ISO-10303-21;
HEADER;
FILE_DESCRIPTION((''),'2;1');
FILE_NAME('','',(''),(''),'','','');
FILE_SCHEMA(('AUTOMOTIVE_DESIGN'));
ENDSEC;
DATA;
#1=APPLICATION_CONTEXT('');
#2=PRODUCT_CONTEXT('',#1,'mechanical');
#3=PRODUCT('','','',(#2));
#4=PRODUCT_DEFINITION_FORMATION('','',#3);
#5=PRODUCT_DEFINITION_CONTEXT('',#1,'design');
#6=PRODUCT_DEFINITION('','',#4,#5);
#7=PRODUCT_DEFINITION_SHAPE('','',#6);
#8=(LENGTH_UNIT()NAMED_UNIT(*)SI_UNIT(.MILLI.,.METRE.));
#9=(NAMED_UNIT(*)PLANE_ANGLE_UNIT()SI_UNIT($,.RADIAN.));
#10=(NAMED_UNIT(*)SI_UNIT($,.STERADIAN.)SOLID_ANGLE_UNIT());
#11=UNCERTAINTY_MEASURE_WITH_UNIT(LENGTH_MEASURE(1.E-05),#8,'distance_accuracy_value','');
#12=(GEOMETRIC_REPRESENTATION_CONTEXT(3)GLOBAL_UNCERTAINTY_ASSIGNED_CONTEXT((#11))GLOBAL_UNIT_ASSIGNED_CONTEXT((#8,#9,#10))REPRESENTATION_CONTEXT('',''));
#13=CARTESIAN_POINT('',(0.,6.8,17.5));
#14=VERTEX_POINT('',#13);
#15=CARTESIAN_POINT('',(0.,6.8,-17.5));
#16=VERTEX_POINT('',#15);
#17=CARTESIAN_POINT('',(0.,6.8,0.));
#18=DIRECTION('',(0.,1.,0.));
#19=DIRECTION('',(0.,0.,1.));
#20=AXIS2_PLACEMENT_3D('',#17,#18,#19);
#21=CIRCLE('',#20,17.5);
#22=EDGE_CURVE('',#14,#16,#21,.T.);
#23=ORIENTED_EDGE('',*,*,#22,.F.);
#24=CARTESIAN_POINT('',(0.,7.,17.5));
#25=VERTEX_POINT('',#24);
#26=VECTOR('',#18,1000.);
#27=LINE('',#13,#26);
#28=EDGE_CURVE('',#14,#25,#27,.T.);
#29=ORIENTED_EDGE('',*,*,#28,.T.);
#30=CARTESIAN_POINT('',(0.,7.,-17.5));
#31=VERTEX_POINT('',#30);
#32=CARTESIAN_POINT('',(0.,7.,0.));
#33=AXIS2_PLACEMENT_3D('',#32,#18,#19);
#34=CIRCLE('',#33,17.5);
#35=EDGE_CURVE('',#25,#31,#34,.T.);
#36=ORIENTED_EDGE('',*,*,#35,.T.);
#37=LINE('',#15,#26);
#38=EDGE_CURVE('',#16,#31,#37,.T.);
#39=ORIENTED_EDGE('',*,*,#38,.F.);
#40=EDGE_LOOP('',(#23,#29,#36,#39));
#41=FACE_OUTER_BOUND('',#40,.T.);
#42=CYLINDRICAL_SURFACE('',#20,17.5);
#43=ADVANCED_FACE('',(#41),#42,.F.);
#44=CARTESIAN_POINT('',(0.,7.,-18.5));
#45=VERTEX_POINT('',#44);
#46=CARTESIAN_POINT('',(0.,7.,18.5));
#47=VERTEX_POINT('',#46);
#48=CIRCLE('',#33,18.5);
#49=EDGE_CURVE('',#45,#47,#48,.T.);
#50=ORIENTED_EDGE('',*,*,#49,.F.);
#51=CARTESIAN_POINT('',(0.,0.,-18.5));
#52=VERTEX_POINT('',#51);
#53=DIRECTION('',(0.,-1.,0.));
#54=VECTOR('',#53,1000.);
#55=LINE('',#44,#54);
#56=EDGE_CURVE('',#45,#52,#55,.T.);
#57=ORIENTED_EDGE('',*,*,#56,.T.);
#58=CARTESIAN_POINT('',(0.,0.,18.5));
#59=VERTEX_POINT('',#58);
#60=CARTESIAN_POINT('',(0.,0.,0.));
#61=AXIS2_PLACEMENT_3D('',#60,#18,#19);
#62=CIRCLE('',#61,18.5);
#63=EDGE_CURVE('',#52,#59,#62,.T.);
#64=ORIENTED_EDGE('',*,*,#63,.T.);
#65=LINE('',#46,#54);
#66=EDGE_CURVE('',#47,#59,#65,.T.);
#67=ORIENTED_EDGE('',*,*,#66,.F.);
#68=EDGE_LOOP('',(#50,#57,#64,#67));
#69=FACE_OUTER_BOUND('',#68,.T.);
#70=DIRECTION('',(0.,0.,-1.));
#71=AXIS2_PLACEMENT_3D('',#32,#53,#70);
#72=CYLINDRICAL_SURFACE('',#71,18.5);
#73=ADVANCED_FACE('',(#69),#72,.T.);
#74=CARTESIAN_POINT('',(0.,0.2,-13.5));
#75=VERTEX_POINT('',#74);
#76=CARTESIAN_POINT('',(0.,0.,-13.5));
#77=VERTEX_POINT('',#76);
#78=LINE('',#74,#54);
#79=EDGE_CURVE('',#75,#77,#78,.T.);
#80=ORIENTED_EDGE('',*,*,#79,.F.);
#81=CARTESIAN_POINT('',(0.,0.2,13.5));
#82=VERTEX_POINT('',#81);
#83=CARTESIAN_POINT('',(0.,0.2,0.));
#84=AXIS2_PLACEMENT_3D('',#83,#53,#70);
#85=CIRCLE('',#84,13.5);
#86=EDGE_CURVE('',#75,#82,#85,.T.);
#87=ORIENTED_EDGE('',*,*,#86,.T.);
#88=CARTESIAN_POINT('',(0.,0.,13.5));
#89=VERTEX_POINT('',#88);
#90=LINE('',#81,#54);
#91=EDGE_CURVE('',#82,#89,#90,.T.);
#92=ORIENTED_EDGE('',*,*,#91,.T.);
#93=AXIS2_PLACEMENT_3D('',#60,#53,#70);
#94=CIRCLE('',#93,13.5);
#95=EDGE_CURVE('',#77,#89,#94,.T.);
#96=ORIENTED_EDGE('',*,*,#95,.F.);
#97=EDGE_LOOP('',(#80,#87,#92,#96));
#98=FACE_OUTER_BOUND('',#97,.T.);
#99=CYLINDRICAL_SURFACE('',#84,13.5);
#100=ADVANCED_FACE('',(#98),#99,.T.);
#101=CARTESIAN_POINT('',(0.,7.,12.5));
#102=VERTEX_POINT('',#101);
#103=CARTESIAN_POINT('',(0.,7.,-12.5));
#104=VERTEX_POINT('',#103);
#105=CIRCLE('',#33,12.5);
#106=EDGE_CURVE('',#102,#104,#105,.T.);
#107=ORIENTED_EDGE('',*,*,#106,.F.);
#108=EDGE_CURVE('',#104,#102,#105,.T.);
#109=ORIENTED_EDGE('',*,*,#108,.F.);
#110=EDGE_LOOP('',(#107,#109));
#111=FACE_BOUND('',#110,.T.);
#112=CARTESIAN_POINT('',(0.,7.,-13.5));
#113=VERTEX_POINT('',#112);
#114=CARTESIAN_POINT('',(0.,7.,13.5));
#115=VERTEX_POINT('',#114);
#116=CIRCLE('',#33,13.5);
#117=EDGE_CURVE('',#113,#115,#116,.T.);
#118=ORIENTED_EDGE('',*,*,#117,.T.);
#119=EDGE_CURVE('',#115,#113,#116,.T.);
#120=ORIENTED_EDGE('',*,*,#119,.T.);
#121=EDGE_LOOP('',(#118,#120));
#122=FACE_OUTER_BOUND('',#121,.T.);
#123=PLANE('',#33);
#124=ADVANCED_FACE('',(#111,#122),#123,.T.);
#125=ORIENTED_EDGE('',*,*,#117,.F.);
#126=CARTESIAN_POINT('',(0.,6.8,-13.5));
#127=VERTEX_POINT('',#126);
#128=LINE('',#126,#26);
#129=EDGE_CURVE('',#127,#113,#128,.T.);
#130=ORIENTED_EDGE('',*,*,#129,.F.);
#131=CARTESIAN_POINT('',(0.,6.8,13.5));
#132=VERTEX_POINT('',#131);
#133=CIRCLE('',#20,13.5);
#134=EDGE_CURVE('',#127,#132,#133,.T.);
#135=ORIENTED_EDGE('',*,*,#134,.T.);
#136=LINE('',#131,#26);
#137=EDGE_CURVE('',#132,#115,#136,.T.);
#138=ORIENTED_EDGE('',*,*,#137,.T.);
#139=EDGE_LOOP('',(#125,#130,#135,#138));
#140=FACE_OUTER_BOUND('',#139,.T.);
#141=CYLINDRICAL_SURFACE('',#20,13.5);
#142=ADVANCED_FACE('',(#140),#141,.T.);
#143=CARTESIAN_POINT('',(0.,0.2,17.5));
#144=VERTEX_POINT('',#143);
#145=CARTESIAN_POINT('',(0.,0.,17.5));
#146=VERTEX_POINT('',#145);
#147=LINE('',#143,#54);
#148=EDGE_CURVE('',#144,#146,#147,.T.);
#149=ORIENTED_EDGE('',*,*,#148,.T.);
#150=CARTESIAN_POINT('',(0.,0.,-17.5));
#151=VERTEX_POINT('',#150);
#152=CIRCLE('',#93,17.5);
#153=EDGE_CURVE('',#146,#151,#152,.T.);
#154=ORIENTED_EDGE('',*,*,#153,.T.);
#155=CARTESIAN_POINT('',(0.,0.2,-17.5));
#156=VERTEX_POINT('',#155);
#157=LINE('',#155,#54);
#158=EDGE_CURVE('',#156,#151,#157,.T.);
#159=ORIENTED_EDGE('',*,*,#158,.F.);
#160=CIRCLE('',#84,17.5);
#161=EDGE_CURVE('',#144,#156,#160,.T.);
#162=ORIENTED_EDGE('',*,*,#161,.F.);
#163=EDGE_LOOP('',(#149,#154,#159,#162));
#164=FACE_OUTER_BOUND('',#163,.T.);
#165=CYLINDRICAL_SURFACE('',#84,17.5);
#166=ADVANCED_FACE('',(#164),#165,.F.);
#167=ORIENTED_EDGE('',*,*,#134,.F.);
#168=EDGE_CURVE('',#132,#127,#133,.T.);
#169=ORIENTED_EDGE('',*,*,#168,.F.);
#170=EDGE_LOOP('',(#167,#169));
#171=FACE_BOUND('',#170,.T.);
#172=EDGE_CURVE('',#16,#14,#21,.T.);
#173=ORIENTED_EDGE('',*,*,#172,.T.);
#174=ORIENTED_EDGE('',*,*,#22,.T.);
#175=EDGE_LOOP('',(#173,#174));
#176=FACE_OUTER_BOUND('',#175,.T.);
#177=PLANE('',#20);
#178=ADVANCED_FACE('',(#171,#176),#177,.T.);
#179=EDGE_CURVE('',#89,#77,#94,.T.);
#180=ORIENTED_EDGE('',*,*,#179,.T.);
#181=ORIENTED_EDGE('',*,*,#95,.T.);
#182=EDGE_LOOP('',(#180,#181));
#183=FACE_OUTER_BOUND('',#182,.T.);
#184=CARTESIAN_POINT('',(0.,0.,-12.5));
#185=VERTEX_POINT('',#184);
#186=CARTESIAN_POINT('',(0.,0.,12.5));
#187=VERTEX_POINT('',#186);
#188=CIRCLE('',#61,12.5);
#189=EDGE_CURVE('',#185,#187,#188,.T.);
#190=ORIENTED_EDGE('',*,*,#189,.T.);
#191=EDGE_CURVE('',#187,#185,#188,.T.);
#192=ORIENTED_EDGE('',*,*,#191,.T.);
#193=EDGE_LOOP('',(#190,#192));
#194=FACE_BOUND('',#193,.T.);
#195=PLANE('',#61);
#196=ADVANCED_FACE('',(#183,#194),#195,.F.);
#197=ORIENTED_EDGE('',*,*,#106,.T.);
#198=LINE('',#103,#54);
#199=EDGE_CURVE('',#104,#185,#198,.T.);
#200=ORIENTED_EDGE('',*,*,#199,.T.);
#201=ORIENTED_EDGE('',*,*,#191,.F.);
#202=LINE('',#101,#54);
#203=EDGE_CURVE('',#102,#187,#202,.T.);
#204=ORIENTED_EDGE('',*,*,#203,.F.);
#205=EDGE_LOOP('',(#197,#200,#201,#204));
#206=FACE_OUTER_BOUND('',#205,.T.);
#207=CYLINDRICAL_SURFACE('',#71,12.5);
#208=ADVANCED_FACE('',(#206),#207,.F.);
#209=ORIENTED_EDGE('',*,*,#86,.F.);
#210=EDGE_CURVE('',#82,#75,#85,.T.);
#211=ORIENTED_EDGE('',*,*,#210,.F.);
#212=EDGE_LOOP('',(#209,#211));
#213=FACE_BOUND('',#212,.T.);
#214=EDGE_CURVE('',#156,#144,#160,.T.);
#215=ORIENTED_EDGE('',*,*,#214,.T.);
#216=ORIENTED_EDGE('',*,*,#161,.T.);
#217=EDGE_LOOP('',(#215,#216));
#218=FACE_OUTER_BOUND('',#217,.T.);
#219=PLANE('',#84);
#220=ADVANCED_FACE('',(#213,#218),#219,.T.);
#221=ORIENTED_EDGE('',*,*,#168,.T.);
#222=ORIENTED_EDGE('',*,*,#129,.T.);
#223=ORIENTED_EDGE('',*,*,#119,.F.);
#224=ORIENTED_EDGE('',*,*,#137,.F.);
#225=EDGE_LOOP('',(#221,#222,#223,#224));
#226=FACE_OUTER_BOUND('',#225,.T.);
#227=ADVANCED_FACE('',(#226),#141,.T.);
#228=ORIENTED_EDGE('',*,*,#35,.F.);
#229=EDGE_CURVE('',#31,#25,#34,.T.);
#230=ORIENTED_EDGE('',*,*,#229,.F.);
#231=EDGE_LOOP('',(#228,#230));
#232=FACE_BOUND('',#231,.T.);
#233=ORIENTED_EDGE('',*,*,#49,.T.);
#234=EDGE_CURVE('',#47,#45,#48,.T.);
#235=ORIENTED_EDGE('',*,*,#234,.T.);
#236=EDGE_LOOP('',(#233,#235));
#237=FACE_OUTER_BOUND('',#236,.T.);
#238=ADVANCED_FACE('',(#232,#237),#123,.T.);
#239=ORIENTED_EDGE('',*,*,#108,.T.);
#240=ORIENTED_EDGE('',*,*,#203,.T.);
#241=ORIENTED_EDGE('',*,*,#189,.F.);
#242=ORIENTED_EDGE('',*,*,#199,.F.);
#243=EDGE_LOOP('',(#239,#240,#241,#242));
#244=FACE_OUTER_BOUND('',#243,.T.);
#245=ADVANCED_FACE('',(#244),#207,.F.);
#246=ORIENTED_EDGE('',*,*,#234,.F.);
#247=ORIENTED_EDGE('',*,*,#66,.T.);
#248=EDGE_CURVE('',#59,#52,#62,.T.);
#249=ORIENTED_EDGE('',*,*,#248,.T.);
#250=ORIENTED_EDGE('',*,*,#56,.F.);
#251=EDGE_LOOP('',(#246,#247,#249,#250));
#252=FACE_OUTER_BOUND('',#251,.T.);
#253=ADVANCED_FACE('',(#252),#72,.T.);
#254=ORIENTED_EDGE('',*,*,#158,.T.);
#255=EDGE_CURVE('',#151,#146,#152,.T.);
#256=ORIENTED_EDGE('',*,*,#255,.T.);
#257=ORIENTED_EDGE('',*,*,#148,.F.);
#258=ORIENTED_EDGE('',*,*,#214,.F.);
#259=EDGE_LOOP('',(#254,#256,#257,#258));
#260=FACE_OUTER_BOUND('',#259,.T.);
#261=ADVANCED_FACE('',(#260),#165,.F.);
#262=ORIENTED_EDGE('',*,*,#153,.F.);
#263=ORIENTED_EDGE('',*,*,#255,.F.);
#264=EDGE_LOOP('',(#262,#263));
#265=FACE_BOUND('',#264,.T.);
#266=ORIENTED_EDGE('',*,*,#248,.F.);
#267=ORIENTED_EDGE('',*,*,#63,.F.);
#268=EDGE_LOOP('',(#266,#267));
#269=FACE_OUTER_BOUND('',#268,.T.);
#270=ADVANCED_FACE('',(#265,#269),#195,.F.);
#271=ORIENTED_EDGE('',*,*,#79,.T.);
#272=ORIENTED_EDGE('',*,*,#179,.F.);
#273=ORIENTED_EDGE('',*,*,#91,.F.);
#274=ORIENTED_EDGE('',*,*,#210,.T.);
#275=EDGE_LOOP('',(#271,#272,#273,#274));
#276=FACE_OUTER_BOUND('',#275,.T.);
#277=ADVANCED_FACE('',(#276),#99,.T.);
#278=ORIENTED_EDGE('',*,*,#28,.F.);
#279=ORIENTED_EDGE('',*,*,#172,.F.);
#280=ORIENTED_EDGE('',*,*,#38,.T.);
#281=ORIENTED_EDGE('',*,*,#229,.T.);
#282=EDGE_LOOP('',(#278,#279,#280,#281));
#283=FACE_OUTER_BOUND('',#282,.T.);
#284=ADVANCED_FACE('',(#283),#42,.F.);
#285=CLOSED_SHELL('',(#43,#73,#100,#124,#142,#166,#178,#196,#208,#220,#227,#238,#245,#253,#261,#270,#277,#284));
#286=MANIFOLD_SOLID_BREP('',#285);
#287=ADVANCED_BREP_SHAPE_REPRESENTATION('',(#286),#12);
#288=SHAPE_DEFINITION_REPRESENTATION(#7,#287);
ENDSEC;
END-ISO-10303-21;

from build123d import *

# Parameters (mm, degrees)
SKETCH1_R           = 18.5
SKETCH1_R_2         = 12.5
BOSS_EXTRUDE1_DEPTH = 7
SKETCH2_R           = 17.5
SKETCH2_R_2         = 13.5
CUT_EXTRUDE1_DEPTH  = 0.2
CUT_EXTRUDE2_START  = -0.2
SKETCH3_R           = 17.5
SKETCH3_R_2         = 13.5
CUT_EXTRUDE2_DEPTH  = 0.2


with BuildPart() as part:
    # Sketch1 → Boss-Extrude1 (new body)
    with BuildSketch(Plane(origin=(0, 0, 0), x_dir=(1, 0, 0), z_dir=(0, 1, 0))):
        with Locations(Location((0, 0, 0), (0, 0, 270))):
            Circle(SKETCH1_R)
        with Locations(Location((0, 0, 0), (0, 0, 270))):
            Circle(SKETCH1_R_2, mode=Mode.SUBTRACT)
    extrude(amount=BOSS_EXTRUDE1_DEPTH)

    # Sketch2 → Cut-Extrude1 (cut)
    with BuildSketch(Plane(origin=(0, 7, 0), x_dir=(1, 0, 0), z_dir=(0, 1, 0))):
        with Locations(Location((0, 0, 0), (0, 0, 270))):
            Circle(SKETCH2_R)
        with Locations(Location((0, 0, 0), (0, 0, 270))):
            Circle(SKETCH2_R_2, mode=Mode.SUBTRACT)
    extrude(amount=-CUT_EXTRUDE1_DEPTH, mode=Mode.SUBTRACT)

    # Sketch3 → Cut-Extrude2 (cut)
    with BuildSketch(Plane.XZ.offset(CUT_EXTRUDE2_START)):
        with Locations(Location((0, 0, 0), (0, 0, 90))):
            Circle(SKETCH3_R)
        with Locations(Location((0, 0, 0), (0, 0, 90))):
            Circle(SKETCH3_R_2, mode=Mode.SUBTRACT)
    extrude(amount=CUT_EXTRUDE2_DEPTH, mode=Mode.SUBTRACT)


solid = part.part
